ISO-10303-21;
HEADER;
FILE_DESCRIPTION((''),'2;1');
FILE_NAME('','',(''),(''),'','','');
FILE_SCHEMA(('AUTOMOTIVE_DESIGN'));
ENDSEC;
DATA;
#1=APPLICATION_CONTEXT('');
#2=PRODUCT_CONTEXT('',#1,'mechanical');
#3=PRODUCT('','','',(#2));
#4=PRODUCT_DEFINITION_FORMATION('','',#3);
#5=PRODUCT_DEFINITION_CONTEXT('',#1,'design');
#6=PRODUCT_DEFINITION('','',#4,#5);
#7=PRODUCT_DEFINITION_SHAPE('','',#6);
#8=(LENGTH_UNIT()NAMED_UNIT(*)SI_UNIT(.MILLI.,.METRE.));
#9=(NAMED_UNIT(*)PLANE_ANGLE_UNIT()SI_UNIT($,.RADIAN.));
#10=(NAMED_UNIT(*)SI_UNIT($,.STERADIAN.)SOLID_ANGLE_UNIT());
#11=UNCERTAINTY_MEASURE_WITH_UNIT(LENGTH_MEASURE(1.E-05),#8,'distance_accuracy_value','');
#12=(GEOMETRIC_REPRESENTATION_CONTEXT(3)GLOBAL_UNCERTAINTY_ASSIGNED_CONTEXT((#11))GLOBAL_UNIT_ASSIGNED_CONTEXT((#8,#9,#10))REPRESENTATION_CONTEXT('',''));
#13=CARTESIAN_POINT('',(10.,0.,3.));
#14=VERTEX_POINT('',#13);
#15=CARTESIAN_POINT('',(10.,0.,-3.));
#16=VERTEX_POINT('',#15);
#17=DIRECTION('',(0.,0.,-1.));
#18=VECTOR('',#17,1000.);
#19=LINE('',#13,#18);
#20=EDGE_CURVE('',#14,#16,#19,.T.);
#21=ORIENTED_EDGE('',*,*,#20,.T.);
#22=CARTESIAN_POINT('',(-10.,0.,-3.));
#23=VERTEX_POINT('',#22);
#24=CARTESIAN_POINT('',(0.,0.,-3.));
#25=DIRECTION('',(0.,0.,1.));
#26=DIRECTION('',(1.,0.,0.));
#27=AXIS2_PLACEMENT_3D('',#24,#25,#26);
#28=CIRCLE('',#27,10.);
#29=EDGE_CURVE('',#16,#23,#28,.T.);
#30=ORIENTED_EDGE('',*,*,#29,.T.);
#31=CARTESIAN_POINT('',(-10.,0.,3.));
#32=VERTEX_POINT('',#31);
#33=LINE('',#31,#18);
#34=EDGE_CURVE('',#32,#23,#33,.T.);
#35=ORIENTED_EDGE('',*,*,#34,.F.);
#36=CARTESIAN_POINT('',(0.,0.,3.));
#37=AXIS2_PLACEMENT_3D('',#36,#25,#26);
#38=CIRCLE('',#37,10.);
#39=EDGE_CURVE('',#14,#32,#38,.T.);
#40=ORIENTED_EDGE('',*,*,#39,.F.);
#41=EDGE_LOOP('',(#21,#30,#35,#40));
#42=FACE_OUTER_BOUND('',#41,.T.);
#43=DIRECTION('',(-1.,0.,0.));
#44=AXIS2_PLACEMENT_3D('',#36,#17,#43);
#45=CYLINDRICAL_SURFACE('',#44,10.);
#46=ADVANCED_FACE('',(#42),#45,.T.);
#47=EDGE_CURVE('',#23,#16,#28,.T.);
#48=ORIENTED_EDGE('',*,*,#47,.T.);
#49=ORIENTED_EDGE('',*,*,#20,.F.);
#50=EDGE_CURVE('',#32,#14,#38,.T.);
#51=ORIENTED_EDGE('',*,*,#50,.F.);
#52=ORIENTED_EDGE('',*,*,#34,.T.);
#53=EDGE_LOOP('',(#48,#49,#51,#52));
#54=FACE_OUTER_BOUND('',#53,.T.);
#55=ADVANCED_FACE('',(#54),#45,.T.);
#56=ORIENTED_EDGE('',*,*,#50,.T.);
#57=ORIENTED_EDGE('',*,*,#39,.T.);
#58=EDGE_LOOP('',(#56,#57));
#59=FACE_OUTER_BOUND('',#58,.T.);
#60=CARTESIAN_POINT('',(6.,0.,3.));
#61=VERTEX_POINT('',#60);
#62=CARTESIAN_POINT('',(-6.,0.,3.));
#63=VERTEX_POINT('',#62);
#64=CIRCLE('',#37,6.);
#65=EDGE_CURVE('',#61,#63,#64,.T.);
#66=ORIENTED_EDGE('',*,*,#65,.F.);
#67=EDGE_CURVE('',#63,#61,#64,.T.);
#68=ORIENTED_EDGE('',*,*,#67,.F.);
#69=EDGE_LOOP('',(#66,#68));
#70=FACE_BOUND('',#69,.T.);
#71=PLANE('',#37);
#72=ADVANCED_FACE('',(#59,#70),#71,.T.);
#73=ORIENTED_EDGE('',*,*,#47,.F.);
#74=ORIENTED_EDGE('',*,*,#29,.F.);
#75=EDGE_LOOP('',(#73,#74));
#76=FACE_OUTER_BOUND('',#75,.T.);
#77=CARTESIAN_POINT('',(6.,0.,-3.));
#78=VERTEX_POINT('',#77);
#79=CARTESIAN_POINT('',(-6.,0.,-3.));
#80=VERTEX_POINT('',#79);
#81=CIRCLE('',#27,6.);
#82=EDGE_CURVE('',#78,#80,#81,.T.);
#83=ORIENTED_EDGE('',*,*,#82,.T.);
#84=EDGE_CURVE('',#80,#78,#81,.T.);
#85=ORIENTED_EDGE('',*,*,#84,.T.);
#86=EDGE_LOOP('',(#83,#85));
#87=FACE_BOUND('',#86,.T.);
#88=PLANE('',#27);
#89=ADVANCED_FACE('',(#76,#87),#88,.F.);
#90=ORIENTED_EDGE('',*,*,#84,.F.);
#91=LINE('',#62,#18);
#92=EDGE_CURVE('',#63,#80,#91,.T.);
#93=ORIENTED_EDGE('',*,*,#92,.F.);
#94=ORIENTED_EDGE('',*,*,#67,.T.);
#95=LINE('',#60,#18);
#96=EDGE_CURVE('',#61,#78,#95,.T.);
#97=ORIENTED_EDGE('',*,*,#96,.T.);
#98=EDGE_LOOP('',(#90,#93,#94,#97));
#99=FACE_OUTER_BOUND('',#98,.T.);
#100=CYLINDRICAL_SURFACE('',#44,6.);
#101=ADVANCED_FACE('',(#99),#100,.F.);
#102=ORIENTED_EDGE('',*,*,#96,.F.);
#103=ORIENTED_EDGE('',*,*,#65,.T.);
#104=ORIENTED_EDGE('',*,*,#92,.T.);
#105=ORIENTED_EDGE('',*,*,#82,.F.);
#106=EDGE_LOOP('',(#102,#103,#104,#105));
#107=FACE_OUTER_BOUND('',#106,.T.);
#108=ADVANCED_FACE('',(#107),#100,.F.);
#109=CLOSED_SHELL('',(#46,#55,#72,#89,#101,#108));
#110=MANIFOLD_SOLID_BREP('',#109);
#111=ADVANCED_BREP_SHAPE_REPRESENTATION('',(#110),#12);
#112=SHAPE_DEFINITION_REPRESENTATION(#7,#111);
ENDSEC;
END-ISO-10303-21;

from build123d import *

# Parameters (mm, degrees)
SKETCH1_R           = 10
SKETCH1_R_2         = 6
BOSS_EXTRUDE1_DEPTH = 3


with BuildPart() as part:
    # Sketch1 → Boss-Extrude1 (new, symmetric)
    with BuildSketch(Plane.XY):
        Circle(SKETCH1_R)
        Circle(SKETCH1_R_2, mode=Mode.SUBTRACT)
    extrude(amount=BOSS_EXTRUDE1_DEPTH, both=True)


solid = part.part
